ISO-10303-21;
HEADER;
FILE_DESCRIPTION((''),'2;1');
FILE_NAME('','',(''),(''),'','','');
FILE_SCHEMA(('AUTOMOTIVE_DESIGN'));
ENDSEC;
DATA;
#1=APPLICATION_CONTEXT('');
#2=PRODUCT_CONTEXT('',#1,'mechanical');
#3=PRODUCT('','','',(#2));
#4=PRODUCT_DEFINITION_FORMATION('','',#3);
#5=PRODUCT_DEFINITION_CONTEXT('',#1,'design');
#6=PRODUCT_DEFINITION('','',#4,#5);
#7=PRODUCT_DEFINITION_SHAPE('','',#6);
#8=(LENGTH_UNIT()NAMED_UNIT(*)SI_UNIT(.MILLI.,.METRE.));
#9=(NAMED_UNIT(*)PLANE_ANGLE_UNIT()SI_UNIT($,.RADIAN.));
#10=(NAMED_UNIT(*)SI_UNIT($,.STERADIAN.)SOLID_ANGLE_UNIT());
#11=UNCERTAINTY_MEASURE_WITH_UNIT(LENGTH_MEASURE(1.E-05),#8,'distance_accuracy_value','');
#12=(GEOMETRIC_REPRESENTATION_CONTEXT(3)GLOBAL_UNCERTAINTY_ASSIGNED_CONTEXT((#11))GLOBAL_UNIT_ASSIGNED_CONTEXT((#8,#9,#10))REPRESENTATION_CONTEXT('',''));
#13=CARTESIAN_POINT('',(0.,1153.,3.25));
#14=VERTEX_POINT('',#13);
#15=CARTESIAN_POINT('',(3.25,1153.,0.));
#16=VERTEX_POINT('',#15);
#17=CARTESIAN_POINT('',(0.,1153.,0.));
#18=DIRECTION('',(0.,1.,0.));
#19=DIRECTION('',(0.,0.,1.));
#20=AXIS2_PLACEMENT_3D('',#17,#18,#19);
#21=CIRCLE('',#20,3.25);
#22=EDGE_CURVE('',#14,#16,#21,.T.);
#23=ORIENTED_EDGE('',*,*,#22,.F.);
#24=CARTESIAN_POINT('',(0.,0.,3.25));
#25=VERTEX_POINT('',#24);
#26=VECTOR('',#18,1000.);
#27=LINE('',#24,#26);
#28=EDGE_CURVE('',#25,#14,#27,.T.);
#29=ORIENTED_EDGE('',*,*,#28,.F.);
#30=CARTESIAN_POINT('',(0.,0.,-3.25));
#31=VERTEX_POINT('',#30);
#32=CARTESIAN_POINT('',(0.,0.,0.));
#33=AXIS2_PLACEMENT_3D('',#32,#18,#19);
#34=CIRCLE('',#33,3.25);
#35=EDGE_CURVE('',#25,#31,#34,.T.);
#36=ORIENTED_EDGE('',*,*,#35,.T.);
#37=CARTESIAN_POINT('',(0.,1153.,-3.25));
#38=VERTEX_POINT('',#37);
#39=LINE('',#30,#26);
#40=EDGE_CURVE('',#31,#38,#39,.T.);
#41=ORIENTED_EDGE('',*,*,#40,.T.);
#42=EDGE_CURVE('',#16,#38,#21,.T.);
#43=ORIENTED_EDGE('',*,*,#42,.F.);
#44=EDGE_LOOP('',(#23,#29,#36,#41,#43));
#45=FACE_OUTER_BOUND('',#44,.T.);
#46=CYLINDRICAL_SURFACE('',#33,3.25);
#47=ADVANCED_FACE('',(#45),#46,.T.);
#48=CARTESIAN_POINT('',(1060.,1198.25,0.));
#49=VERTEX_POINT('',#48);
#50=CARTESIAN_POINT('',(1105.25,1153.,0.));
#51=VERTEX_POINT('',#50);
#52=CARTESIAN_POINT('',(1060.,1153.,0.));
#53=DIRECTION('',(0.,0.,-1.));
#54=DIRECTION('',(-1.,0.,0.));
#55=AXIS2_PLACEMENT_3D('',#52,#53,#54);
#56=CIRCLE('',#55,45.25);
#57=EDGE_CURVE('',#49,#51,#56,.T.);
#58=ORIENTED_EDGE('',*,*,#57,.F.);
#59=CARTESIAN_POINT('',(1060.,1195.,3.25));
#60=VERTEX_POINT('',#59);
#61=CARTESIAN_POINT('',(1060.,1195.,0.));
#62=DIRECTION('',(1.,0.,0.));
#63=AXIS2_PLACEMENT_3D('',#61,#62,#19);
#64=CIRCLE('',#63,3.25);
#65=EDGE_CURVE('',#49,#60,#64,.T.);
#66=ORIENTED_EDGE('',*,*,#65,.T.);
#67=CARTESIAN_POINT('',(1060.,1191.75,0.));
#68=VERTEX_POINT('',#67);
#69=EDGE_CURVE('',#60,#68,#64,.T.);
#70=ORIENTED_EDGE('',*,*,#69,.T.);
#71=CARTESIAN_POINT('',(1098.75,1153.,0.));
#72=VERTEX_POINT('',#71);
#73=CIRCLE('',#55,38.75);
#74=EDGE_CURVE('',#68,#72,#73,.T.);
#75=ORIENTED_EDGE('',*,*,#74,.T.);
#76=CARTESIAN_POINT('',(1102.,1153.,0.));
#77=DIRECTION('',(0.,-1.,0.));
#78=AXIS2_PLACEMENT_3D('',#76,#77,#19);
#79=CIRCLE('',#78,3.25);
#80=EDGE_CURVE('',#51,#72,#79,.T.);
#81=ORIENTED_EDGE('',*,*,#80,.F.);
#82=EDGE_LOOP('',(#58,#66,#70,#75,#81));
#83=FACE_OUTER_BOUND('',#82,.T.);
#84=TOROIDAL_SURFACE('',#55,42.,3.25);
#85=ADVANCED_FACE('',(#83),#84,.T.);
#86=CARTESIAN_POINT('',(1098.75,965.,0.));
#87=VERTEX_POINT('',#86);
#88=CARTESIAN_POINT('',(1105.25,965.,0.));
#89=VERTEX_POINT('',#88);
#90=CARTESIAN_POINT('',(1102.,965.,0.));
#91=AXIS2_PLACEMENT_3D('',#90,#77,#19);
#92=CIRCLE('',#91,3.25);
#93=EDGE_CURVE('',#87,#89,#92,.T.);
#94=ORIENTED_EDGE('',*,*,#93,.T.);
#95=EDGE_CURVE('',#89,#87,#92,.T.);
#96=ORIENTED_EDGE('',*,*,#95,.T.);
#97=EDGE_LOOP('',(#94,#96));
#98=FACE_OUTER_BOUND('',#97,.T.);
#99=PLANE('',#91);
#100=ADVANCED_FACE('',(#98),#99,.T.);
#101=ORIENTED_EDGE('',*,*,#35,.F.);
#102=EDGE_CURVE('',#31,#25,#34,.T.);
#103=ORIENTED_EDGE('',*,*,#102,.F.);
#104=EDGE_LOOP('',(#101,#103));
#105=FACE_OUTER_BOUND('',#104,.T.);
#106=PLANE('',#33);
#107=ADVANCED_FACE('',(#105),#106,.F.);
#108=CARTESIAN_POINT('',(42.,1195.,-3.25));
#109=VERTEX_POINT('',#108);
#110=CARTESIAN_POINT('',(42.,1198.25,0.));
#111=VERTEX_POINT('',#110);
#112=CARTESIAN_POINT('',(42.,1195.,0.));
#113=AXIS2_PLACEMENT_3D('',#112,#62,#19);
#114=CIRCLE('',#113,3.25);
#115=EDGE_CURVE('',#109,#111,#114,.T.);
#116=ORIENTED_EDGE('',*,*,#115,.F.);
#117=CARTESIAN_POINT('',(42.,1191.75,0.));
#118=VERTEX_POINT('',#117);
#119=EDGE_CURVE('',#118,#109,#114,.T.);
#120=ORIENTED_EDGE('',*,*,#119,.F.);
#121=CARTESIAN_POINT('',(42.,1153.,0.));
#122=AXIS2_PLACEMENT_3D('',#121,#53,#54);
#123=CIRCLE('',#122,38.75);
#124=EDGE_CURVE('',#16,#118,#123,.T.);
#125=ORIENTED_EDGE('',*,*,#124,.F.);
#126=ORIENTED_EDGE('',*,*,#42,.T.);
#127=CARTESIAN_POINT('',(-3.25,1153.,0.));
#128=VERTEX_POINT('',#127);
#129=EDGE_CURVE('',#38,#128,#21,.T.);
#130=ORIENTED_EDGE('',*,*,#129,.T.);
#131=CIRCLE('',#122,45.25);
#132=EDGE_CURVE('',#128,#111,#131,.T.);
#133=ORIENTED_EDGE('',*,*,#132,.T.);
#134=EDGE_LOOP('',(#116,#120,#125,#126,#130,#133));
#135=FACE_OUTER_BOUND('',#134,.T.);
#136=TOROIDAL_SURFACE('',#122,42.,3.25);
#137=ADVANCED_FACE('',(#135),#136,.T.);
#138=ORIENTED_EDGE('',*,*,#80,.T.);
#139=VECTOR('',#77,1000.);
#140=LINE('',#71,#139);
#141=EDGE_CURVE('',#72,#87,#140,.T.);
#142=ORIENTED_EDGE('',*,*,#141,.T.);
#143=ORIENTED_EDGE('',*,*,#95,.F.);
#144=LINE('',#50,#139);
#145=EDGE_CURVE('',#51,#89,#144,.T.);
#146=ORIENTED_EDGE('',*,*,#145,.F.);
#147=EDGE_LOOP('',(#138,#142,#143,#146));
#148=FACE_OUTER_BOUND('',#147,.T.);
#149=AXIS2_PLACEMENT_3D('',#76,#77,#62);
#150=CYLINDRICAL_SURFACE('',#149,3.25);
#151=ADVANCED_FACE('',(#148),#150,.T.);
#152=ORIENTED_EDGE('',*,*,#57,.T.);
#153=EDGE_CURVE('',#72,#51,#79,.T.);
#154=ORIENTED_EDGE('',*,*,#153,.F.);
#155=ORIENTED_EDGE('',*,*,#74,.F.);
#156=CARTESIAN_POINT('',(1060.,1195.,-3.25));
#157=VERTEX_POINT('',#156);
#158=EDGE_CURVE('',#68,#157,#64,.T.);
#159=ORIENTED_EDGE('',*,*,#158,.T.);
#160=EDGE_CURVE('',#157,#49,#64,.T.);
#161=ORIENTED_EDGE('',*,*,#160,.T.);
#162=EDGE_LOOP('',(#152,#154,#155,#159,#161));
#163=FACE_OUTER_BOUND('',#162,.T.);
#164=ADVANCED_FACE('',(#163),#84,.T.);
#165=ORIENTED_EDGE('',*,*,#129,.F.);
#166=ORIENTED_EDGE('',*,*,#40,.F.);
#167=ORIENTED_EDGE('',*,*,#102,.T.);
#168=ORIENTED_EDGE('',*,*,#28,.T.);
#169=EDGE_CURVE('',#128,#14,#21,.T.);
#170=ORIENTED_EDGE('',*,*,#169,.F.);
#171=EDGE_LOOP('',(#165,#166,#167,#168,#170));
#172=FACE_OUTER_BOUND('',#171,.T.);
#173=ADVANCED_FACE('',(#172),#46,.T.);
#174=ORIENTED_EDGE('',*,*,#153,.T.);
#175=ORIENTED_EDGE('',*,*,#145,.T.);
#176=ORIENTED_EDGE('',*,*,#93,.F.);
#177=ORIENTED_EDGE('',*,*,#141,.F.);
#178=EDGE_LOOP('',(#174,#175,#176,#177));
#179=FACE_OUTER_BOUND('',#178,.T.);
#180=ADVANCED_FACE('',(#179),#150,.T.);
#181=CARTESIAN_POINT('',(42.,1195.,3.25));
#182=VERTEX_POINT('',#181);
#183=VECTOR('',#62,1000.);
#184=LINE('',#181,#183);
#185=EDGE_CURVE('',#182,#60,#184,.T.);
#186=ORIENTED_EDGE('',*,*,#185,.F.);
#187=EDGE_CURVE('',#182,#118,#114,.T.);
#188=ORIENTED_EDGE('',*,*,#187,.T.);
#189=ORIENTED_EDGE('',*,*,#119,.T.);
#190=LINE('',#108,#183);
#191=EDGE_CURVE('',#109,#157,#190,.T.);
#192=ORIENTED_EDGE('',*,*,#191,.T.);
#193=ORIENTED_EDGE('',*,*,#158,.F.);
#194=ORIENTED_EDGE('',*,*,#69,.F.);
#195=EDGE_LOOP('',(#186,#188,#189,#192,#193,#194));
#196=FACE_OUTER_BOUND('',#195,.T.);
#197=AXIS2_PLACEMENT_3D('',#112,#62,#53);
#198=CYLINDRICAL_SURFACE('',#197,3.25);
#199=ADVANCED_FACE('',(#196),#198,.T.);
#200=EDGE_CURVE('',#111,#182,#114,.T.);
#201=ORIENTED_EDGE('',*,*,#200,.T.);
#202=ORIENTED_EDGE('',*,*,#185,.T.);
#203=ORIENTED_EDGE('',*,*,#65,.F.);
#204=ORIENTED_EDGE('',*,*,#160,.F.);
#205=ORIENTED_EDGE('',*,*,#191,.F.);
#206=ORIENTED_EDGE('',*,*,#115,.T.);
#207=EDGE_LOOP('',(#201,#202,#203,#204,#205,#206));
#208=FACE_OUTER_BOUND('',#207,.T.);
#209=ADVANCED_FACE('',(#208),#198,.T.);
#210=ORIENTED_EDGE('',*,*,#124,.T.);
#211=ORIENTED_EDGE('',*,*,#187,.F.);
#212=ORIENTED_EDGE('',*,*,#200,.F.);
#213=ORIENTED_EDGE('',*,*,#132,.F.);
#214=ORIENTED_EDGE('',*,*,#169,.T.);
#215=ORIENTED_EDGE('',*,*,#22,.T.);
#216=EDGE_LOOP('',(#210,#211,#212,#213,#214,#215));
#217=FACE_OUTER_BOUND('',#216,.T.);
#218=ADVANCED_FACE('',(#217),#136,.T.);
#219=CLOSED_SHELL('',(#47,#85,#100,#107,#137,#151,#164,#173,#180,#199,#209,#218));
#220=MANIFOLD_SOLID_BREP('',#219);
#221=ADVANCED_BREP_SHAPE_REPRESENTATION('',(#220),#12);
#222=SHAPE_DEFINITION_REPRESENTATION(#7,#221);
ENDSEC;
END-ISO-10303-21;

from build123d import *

# Parameters (mm, degrees)
SKETCH2_R = 3.25


with BuildPart() as part:
    # Sweep1: sweep along a path in Sketch1
    with BuildLine(Plane.XY) as sweep1_path:
        Line((0, 0), (0, 1153))
        ThreePointArc((0, 1153), (12.30151519, 1182.69848481), (42, 1195))
        Line((42, 1195), (1060, 1195))
        ThreePointArc((1060, 1195), (1089.69848481, 1182.69848481), (1102, 1153))
        Line((1102, 1153), (1102, 965))
    # Sketch2 → Sweep1 (sweep)
    with BuildSketch(Plane(origin=(0, 0, 0), x_dir=(1, 0, 0), z_dir=(0, 1, 0))):
        Circle(SKETCH2_R)
    sweep(path=sweep1_path.line)


solid = part.part
